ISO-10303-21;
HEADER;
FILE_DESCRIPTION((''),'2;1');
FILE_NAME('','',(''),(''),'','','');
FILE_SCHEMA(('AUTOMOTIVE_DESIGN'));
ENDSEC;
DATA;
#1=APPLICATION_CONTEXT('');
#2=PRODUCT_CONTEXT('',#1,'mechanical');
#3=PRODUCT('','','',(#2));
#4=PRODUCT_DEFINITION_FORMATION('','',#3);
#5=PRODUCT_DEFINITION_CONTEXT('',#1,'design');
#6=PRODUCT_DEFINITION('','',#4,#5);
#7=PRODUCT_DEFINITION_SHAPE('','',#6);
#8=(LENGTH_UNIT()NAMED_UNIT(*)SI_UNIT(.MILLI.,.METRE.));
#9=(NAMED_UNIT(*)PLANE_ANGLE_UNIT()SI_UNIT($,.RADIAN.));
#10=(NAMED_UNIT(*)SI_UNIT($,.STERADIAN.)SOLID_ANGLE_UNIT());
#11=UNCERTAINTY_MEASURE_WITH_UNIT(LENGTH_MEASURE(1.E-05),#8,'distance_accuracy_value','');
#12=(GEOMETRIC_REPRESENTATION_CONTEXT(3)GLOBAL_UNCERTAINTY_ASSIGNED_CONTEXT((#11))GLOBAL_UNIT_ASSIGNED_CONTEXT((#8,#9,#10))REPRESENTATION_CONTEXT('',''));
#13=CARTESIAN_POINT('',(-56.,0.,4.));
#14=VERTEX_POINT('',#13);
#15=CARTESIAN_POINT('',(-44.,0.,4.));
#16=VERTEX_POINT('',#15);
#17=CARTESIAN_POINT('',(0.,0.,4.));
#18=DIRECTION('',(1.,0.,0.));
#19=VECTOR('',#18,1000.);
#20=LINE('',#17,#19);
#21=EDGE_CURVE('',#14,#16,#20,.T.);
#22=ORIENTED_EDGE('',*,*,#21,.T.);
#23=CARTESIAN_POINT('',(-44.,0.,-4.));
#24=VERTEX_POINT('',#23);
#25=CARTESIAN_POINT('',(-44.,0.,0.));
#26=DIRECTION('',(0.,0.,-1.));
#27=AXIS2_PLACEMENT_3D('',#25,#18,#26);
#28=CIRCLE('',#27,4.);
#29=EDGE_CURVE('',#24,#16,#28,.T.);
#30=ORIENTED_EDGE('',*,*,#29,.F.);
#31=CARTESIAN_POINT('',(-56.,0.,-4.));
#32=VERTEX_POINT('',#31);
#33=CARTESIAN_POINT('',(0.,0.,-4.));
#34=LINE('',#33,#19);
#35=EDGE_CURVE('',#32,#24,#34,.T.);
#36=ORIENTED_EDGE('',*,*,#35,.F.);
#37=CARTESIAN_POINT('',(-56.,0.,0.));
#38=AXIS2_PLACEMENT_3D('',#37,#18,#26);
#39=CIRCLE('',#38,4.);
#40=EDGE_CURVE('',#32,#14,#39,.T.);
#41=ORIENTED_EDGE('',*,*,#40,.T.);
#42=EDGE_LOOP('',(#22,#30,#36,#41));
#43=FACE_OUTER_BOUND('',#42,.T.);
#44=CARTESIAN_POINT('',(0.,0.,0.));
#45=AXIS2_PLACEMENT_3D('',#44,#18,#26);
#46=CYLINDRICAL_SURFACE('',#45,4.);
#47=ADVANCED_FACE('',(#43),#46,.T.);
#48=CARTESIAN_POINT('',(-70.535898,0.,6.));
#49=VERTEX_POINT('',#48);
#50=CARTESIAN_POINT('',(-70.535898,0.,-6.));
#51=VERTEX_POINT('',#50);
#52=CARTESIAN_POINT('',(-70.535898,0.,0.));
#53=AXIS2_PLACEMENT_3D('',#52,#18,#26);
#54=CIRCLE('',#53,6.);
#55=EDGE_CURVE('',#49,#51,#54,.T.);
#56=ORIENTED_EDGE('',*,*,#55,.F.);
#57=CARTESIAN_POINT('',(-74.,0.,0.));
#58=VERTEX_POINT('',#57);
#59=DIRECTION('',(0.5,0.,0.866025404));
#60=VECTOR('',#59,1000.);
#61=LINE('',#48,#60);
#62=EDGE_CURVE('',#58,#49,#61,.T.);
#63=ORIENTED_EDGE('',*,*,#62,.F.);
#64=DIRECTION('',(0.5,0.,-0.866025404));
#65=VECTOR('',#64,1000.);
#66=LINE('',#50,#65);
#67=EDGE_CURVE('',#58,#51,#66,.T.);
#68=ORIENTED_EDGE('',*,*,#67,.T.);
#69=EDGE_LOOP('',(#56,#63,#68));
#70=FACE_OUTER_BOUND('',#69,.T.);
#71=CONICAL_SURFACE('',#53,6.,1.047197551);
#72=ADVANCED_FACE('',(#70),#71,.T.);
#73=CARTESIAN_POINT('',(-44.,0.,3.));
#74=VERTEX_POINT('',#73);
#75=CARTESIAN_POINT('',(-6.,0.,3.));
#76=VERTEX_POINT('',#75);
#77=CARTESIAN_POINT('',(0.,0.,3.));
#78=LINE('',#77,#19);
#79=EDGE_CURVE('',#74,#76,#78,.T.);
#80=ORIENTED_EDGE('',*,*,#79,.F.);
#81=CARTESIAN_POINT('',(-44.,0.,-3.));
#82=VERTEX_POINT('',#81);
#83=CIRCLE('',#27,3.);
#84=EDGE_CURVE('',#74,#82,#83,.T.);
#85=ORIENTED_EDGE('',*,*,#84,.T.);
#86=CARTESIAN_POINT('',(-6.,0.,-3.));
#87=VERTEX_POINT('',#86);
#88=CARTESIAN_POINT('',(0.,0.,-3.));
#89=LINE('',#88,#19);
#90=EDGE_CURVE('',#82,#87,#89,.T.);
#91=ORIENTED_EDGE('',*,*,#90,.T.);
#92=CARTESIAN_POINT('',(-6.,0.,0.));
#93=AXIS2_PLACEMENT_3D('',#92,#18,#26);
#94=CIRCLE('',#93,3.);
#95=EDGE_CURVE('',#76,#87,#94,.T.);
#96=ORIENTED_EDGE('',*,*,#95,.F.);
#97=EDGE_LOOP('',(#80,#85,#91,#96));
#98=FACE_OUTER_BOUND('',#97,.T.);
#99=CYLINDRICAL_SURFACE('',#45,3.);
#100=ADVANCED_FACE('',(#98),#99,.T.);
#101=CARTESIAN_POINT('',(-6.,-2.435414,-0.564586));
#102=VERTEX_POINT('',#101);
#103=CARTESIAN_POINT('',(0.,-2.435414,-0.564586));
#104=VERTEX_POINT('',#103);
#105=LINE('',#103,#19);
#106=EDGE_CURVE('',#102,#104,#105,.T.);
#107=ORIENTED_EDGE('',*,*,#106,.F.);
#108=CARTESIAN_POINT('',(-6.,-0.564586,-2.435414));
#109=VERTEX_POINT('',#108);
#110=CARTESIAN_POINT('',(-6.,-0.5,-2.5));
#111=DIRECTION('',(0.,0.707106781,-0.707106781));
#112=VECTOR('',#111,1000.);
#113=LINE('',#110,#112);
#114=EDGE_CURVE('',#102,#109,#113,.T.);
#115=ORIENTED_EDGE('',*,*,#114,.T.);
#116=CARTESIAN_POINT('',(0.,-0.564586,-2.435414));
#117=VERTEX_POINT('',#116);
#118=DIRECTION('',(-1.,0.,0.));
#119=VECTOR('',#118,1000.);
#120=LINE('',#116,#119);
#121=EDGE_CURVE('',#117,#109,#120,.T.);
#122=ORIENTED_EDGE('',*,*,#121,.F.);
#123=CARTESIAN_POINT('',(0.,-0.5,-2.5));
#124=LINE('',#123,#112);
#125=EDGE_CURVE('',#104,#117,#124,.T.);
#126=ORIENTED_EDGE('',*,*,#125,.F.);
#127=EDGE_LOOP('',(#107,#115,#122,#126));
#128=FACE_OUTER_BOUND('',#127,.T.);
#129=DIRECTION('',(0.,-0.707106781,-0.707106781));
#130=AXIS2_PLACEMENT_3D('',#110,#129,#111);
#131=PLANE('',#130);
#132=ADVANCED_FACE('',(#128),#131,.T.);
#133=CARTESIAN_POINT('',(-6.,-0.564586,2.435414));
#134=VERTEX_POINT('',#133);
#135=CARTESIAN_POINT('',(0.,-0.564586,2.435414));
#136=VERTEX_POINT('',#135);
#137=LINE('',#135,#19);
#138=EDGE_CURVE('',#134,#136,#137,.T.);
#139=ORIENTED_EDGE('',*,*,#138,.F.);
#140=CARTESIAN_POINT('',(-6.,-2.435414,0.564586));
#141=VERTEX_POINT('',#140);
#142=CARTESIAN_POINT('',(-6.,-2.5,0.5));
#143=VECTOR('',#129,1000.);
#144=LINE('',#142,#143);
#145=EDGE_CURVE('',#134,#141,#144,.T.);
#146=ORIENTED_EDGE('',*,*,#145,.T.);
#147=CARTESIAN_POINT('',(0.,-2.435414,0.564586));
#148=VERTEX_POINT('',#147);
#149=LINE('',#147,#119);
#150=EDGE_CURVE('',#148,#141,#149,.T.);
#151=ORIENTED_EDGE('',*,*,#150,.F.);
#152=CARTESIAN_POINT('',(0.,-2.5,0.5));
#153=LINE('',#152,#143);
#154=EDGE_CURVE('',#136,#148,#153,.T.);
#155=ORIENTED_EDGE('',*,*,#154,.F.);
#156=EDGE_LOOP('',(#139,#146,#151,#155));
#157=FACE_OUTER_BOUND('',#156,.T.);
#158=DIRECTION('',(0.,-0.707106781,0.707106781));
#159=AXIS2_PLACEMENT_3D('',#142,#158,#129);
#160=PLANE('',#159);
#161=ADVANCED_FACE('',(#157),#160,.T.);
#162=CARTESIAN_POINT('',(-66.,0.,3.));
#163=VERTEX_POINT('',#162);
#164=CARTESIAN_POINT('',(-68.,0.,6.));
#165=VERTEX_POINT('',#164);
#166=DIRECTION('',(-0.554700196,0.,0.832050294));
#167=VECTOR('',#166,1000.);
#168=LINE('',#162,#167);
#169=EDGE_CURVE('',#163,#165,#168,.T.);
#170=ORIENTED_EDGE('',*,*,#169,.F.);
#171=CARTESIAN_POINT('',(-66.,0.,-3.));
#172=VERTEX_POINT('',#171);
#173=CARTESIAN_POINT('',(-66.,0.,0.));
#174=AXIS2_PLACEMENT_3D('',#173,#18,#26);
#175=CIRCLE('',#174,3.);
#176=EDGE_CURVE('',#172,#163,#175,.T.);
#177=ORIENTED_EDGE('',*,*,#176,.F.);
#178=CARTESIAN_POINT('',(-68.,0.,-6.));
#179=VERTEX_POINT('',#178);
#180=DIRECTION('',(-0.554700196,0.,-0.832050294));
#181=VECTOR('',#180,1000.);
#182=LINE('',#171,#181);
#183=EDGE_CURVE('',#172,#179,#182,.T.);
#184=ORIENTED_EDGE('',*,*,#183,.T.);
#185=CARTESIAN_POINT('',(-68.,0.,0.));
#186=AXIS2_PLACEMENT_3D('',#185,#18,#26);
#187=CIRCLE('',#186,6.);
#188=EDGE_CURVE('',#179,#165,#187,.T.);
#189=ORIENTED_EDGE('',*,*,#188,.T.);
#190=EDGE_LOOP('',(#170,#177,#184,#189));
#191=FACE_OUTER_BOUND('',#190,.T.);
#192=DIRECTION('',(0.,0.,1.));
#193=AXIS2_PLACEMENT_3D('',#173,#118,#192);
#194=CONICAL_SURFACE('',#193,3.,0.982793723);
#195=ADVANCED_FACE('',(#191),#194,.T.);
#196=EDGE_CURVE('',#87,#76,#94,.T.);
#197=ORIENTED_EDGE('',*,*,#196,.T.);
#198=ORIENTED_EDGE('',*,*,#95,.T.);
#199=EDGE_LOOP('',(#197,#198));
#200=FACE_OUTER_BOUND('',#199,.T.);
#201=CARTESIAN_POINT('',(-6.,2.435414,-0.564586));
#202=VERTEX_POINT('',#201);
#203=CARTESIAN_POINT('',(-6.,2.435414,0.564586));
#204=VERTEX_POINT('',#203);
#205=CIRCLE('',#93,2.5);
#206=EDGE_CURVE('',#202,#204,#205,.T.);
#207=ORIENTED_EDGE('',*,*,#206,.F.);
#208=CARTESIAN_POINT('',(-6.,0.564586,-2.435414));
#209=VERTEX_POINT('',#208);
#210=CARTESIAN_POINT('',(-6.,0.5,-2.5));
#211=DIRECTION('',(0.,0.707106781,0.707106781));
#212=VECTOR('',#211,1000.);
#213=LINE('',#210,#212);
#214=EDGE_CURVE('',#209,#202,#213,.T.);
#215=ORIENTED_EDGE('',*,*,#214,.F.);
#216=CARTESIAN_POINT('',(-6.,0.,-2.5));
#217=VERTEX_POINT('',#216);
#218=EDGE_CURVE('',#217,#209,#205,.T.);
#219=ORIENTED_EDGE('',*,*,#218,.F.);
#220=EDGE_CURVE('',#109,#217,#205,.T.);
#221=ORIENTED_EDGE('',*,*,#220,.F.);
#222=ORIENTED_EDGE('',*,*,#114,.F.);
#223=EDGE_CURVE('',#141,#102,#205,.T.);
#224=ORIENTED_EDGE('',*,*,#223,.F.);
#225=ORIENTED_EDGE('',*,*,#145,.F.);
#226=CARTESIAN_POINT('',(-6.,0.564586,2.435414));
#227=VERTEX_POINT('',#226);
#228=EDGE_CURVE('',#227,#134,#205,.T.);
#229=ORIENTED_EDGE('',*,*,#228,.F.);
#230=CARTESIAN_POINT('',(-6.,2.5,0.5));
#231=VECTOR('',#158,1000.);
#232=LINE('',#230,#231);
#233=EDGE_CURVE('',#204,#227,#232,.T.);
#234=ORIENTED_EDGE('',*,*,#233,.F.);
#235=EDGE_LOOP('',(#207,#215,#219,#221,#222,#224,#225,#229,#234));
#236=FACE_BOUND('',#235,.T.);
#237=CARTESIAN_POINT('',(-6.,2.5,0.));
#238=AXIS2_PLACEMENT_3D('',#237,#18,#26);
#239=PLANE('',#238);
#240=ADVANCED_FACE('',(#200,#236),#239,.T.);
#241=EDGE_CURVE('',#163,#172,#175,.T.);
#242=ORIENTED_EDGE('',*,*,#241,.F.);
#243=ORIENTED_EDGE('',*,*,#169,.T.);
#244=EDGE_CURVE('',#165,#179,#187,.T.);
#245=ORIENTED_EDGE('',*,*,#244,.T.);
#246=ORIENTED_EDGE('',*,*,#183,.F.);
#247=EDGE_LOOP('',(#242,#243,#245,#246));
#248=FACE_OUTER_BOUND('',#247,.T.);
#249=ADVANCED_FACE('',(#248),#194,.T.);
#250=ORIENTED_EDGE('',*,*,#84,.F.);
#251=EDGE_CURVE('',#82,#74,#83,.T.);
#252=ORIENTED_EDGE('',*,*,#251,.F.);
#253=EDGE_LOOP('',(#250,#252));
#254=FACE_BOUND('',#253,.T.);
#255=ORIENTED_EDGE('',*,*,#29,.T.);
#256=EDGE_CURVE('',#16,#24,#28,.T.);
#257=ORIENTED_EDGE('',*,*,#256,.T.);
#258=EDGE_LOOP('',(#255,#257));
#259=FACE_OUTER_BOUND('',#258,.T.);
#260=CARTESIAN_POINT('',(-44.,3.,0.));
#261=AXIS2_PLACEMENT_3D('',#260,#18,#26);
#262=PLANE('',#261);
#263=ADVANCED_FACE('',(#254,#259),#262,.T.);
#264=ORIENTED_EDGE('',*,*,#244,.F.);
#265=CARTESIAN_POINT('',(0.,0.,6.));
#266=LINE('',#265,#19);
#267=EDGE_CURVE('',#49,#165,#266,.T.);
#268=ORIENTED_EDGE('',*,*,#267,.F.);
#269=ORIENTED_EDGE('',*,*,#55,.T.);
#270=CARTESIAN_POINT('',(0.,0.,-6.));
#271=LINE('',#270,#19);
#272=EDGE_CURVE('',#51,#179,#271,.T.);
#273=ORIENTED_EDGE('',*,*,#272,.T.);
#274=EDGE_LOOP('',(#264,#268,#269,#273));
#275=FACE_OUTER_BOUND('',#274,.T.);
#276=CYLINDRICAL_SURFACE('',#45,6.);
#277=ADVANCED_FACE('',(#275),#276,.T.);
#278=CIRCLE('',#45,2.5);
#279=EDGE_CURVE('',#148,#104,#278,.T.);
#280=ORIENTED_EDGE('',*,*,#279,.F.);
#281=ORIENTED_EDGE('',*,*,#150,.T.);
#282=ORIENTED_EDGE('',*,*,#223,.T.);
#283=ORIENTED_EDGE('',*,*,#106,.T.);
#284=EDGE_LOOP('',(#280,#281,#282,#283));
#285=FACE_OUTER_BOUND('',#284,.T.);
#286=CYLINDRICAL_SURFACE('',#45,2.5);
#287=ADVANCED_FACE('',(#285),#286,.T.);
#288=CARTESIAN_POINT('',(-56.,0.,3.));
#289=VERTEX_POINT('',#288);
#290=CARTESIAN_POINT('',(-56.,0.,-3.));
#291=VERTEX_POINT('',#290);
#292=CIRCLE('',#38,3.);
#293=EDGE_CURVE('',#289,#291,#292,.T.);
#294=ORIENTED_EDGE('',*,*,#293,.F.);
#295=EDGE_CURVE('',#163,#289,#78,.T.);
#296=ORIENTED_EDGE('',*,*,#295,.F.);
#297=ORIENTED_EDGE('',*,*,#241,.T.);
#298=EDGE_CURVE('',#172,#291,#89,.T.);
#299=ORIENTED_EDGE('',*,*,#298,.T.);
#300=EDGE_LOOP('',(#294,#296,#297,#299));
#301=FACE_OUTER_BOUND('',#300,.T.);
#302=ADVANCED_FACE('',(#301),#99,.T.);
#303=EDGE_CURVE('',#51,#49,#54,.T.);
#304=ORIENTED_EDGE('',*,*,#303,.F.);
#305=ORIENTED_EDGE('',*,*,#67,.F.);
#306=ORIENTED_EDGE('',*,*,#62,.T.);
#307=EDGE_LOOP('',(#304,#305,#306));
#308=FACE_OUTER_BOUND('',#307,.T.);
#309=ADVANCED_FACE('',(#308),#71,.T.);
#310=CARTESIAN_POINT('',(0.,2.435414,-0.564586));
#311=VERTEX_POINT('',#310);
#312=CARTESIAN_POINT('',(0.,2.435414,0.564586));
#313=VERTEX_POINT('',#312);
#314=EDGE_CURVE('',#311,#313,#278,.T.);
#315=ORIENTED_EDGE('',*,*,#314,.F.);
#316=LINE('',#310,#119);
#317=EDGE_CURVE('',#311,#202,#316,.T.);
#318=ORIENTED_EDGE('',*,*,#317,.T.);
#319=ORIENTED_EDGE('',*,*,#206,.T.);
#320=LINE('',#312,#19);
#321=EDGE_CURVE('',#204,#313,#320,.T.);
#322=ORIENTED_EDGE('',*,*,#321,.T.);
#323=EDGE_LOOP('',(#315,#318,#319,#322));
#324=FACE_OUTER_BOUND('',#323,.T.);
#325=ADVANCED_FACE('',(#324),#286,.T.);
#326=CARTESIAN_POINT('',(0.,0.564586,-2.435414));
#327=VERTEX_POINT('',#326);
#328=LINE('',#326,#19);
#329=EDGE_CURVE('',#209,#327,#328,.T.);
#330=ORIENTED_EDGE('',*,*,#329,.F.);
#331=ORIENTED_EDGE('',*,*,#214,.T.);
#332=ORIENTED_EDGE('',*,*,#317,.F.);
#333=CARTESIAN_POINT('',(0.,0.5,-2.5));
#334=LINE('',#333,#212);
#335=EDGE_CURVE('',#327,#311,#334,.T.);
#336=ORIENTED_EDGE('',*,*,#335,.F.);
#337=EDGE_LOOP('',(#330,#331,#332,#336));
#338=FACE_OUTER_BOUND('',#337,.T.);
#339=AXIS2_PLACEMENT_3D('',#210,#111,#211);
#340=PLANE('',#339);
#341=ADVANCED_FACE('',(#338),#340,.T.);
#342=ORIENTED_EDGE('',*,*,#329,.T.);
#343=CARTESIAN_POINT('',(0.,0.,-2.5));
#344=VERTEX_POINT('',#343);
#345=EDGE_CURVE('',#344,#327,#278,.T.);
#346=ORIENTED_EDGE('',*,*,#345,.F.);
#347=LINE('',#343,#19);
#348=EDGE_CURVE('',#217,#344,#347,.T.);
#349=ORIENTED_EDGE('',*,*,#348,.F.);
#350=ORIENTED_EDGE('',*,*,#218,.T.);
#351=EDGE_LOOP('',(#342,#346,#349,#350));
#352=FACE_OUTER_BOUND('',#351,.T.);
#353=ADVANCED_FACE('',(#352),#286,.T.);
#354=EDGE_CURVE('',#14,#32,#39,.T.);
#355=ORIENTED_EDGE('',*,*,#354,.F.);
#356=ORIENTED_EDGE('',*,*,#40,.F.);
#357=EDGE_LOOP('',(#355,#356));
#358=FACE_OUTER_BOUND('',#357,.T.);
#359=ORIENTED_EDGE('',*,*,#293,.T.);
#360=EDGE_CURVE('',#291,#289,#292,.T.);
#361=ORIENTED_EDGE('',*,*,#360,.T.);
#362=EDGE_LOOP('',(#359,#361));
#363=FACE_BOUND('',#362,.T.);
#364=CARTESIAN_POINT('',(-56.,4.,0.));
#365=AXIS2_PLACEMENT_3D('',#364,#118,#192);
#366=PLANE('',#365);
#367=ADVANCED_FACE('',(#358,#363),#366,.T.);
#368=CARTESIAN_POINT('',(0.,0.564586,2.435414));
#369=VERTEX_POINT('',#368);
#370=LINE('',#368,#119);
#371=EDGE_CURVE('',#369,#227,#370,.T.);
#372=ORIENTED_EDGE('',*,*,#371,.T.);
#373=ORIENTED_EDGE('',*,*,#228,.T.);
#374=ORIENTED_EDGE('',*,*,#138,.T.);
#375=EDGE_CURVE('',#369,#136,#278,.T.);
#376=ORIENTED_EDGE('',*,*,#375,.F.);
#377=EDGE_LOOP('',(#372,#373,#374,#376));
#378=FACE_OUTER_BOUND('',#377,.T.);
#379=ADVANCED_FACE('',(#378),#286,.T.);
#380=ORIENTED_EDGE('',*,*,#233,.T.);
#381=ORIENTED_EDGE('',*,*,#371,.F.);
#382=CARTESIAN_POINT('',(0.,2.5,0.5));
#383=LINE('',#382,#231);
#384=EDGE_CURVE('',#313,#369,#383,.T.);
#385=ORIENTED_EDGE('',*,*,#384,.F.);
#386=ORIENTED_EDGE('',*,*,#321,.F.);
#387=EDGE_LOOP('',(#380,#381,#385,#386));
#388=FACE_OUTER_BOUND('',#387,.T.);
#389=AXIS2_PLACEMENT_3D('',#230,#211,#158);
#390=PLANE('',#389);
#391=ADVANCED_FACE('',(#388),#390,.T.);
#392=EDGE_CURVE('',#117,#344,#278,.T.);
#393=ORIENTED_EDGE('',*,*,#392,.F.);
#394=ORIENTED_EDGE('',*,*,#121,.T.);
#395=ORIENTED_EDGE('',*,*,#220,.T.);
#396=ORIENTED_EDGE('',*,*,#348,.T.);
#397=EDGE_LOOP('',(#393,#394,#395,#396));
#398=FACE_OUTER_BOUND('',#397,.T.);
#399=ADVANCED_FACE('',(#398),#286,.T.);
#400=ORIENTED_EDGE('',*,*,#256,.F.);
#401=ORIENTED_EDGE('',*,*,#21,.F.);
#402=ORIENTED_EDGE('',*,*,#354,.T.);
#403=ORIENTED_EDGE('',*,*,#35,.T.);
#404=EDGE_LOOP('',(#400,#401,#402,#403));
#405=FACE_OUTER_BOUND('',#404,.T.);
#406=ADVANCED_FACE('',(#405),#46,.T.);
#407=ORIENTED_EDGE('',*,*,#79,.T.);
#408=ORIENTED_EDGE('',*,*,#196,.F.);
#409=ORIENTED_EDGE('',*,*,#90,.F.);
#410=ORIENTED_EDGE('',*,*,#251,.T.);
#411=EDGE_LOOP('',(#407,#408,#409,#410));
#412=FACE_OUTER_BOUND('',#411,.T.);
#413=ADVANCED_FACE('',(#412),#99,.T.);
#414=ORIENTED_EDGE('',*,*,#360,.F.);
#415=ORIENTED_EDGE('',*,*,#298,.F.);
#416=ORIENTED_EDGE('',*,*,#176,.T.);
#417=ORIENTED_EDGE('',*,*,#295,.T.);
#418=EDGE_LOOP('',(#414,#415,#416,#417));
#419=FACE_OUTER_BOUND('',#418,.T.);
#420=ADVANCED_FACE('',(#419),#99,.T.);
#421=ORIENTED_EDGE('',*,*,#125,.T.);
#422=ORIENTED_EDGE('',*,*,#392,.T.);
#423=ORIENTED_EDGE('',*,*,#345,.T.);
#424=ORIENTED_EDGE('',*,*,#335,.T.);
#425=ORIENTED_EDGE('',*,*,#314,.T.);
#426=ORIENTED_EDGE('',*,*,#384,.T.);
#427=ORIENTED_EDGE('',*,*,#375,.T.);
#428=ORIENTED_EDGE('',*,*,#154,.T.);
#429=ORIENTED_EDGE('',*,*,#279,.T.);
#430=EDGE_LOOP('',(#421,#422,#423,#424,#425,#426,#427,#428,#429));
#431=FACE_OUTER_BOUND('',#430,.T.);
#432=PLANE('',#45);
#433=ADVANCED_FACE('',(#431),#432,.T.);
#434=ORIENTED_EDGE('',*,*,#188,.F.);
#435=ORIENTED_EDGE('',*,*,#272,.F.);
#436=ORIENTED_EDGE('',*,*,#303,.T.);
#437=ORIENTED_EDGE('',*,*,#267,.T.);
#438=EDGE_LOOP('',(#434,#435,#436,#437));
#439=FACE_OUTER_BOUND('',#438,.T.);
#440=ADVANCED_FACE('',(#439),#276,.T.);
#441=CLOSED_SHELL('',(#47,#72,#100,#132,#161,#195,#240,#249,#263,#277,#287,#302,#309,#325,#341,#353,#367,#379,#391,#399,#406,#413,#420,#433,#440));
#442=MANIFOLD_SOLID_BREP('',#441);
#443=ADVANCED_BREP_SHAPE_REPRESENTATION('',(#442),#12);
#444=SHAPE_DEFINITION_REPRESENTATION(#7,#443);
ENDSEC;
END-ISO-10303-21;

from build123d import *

# Parameters (mm, degrees)
SQUARE_DRIVE_SKETCH_OUTSIDE_W = 29.184
SQUARE_DRIVE_SKETCH_OUTSIDE_H = 29.184
SQUARE_DRIVE_5X5_CUT_DEPTH    = 6


with BuildPart() as part:
    # Spindle Profile Sketch → Spindle Body Revolve (revolve)
    with BuildSketch(Plane.XY, mode=Mode.PRIVATE) as spindle_body_revolve_sk:
        Polygon((0, 0), (0, 2.5), (-6, 2.5), (-6, 3), (-44, 3), (-44, 4), (-56, 4), (-56, 3), (-66, 3), (-68, 6), (-70.535898385, 6), (-74, 0), align=None)
    revolve(spindle_body_revolve_sk.sketch.rotate(Axis((0, 0, 0), (-1, 0, 0)), 90), axis=Axis((0, 0, 0), (-1, 0, 0)))

    # Square Drive Sketch outside → Square Drive 5x5 Cut (cut)
    with BuildSketch(Plane(origin=(0, 0, 0), x_dir=(0, 0, -1), z_dir=(1, 0, 0))):
        Rectangle(SQUARE_DRIVE_SKETCH_OUTSIDE_W, SQUARE_DRIVE_SKETCH_OUTSIDE_H)
        Polygon((-0.5, 2.5), (-2.5, 0.5), (-2.5, -0.5), (-0.5, -2.5), (0.5, -2.5), (2.5, -0.5), (2.5, 0.5), (0.5, 2.5), align=None, mode=Mode.SUBTRACT)
    extrude(amount=-SQUARE_DRIVE_5X5_CUT_DEPTH, mode=Mode.SUBTRACT)


solid = part.part
